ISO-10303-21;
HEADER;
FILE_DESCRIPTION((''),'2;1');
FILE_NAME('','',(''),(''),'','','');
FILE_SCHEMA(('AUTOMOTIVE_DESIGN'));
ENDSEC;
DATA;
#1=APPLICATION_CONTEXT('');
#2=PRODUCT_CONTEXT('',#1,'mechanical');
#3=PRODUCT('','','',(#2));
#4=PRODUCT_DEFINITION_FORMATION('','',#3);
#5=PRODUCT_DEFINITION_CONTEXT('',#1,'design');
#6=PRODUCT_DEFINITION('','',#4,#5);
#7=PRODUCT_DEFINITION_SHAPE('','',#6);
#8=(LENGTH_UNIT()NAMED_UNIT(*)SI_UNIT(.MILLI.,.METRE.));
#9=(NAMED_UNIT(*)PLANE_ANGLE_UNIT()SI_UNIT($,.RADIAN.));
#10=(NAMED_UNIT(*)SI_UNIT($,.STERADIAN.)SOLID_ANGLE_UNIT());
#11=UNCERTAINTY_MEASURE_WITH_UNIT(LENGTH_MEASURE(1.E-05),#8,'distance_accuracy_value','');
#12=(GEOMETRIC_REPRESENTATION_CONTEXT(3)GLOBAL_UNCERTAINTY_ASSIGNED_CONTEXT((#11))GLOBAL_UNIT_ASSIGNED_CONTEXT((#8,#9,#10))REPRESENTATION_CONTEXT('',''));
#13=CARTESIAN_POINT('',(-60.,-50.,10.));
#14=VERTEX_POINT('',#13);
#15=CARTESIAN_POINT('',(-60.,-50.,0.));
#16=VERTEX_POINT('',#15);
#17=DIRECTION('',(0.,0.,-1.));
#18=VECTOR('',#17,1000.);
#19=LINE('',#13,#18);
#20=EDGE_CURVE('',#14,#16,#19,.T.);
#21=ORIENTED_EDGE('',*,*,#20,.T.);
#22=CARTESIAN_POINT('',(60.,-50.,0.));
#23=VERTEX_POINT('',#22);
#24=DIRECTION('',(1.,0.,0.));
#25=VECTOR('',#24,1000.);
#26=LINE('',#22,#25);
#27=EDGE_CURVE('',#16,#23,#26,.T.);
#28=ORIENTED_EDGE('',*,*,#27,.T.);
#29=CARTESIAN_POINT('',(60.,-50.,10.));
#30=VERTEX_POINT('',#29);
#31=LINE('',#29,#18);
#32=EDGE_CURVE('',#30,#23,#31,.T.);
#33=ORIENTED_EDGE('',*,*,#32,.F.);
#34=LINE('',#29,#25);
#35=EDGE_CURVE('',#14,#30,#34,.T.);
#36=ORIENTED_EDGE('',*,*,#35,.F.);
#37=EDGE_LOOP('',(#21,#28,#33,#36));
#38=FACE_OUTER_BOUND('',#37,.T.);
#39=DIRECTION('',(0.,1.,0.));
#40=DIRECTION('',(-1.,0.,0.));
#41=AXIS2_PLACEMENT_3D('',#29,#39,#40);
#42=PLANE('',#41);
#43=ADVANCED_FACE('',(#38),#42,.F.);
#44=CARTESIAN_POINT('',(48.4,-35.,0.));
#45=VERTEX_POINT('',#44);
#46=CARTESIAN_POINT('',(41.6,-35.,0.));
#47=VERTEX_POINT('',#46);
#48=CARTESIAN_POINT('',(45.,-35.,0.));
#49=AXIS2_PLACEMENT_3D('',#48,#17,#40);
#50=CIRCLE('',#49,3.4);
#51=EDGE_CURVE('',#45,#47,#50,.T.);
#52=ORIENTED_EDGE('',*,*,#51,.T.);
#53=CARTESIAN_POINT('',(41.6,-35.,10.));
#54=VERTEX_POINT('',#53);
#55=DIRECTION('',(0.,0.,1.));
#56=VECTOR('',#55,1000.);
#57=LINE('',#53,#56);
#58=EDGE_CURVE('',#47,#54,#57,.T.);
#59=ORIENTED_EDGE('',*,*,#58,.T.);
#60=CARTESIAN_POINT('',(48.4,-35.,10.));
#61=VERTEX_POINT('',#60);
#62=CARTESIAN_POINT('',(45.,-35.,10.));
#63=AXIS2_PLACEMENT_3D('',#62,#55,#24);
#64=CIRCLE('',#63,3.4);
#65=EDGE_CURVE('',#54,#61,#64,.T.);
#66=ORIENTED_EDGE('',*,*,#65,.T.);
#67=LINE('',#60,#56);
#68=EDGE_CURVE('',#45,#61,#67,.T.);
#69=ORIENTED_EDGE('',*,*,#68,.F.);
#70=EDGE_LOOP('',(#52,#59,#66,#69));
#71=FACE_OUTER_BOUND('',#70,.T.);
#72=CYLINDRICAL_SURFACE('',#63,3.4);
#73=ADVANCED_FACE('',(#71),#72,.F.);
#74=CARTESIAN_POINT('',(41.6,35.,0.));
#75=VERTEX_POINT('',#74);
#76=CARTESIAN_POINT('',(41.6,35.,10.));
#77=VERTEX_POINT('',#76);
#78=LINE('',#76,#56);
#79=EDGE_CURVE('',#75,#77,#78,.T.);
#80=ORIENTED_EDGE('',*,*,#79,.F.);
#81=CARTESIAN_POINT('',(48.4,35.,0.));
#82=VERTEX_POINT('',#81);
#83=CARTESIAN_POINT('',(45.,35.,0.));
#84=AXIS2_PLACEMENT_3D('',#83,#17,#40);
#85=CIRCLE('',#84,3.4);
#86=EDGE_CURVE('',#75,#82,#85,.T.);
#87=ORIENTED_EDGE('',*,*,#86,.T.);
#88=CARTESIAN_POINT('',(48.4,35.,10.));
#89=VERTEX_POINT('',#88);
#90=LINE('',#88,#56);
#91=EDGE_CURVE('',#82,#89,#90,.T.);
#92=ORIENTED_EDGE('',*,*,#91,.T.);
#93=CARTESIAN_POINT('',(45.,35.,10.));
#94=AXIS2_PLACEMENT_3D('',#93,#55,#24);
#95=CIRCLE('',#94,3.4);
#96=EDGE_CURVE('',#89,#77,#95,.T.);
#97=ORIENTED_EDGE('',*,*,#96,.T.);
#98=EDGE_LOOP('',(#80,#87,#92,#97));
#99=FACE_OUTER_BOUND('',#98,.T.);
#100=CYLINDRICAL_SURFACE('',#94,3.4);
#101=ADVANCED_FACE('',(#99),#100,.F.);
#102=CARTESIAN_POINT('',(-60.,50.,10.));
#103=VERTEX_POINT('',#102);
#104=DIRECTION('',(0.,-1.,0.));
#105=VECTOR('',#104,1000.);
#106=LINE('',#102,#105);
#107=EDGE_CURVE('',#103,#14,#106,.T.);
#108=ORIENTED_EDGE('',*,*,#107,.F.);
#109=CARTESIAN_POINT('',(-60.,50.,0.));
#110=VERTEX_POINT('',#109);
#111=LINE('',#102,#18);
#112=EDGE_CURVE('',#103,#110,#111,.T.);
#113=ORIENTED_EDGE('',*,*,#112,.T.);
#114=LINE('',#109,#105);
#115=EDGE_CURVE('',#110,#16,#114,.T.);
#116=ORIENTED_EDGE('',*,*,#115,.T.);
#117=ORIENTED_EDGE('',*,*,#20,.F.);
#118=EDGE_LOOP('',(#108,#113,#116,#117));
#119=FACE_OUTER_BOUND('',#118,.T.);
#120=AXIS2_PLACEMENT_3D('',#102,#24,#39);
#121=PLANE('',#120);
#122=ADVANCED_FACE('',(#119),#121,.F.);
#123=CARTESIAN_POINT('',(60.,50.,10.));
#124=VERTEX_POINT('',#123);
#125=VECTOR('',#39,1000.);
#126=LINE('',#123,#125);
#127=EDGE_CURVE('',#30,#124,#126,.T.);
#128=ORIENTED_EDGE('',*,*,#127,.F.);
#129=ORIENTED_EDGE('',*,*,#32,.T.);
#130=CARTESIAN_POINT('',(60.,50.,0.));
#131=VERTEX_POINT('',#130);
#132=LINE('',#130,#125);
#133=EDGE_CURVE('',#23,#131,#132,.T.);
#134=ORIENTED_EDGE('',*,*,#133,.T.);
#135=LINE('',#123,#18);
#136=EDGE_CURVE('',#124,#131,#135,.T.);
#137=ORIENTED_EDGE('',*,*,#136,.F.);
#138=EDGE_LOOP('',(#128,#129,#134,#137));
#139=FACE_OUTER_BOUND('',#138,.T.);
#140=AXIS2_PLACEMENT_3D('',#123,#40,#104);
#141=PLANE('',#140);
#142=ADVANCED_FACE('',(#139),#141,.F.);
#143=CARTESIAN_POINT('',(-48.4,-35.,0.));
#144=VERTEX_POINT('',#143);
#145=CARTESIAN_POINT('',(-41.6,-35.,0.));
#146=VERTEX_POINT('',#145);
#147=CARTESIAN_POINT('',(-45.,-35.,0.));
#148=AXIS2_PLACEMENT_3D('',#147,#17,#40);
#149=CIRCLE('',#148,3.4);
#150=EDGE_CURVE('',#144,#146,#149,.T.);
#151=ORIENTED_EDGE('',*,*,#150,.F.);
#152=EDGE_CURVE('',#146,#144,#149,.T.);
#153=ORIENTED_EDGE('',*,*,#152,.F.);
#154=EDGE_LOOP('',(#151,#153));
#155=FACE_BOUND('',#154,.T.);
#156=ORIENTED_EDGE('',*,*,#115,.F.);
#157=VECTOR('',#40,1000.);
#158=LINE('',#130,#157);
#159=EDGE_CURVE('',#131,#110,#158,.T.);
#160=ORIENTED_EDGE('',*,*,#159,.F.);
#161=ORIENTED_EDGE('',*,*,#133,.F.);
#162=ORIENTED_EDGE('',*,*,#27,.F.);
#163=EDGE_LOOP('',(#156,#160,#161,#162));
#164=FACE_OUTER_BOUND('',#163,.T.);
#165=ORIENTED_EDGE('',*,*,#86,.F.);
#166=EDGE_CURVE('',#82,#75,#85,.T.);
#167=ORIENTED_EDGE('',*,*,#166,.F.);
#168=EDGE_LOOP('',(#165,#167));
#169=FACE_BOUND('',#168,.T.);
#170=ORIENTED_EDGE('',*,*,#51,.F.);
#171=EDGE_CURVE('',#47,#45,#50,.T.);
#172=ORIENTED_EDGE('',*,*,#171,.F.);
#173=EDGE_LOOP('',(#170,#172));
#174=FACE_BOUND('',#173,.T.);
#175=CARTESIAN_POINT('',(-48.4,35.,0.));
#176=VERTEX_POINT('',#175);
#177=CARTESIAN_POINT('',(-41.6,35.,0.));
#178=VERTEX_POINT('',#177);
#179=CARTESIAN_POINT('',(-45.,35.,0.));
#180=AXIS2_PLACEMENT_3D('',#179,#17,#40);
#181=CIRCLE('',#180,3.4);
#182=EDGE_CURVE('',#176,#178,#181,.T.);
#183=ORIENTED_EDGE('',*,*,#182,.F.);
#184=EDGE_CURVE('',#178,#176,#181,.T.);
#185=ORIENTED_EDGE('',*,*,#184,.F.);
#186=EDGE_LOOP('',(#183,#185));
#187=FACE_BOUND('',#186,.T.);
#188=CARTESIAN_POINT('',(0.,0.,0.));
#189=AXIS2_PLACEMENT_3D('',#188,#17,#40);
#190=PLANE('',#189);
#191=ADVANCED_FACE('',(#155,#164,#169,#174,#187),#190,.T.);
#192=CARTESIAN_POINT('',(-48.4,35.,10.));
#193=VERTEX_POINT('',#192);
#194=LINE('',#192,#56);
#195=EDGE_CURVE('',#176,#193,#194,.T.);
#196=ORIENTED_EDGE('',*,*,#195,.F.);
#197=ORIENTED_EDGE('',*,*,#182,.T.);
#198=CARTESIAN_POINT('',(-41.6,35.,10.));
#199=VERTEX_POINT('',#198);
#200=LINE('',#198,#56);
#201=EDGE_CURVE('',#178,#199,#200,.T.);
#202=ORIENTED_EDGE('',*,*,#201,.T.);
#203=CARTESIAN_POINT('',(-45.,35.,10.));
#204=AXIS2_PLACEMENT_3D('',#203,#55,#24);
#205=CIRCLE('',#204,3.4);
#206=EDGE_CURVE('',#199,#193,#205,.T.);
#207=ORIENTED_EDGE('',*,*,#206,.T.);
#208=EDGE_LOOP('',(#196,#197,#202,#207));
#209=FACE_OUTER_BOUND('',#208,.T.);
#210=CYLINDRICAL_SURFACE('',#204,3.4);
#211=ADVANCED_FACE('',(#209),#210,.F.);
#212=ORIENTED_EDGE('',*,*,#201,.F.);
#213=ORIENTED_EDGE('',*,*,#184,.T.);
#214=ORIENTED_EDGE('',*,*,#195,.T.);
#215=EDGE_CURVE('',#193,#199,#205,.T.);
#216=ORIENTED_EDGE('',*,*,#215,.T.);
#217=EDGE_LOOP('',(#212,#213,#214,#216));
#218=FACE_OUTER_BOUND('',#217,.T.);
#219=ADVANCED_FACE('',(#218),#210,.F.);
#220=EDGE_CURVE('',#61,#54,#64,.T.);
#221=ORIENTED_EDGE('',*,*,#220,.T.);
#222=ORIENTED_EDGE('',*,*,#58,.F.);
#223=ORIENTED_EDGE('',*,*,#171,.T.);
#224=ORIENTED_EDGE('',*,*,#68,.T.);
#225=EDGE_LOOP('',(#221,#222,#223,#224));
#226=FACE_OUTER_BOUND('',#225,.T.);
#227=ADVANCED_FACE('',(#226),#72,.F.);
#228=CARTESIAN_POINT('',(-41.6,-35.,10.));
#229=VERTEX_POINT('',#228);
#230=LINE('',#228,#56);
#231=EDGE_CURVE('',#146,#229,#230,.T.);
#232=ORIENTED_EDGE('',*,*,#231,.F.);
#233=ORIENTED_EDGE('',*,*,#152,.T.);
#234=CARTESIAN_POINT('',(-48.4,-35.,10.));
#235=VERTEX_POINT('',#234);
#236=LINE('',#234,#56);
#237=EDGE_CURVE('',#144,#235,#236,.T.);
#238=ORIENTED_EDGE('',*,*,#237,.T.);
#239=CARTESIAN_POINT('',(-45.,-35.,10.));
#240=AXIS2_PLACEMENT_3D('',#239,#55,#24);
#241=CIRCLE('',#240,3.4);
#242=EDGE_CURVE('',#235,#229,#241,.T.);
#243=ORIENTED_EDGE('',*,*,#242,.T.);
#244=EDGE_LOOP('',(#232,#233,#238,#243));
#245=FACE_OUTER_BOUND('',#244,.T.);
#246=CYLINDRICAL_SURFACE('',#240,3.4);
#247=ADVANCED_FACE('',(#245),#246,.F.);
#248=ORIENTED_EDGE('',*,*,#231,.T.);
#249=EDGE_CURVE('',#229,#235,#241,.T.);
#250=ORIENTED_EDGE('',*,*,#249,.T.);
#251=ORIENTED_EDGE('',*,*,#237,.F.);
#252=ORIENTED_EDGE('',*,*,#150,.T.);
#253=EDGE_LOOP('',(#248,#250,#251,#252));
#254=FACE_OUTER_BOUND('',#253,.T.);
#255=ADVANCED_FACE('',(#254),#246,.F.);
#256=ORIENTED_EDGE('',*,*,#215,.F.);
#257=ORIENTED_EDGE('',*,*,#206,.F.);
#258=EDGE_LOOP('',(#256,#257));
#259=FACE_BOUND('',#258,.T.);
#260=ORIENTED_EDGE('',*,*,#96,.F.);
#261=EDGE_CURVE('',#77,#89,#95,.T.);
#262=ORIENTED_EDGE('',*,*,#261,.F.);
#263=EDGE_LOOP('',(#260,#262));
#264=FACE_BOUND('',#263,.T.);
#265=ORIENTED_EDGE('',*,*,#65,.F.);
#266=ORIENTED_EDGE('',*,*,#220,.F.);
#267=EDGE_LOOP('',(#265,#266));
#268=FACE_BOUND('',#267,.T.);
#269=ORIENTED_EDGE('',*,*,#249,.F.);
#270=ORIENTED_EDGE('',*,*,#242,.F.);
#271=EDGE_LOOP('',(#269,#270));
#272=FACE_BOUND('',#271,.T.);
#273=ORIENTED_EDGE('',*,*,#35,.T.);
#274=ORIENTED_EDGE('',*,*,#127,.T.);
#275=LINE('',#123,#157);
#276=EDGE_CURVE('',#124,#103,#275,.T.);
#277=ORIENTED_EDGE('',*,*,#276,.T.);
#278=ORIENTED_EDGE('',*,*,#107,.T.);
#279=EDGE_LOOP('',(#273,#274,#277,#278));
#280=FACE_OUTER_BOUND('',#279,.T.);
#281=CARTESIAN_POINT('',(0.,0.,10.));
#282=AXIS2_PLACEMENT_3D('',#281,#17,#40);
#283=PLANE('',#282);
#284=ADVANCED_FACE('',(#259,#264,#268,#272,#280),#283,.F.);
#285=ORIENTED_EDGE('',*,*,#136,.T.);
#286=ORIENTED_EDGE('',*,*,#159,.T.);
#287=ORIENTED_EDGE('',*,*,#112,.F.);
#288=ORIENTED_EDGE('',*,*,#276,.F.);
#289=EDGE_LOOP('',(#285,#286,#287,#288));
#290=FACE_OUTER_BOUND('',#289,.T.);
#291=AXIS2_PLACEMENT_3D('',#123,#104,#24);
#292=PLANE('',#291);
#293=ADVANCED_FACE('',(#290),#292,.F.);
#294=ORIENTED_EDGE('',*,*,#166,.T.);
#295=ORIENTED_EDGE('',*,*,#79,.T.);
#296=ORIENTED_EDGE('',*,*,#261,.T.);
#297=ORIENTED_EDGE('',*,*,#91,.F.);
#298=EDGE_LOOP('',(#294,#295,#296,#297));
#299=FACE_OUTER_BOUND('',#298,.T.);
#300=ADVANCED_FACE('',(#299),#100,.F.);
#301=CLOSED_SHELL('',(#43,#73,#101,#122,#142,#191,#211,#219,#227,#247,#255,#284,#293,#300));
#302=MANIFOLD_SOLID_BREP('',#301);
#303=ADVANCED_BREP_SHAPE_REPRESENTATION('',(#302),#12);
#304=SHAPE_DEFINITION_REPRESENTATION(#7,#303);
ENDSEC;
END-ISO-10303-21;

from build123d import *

# Parameters (mm, degrees)
SKETCH1_W             = 120
SKETCH1_H             = 100
BOSS_EXTRUDE1_DEPTH   = 10
M8_TAPPED_HOLE1_D     = 6.8
M8_TAPPED_HOLE1_DEPTH = 19.75
M8_TAPPED_HOLE1_TIP   = 2.042926105


with BuildPart() as part:
    # Sketch1 → Boss-Extrude1 (new body)
    with BuildSketch(Plane.XY):
        Rectangle(SKETCH1_W, SKETCH1_H)
    extrude(amount=BOSS_EXTRUDE1_DEPTH)

    # M8 Tapped Hole1
    with Locations(Plane.XY.offset(10)):
        with Locations((45, -35), (-45, -35), (-45, 35), (45, 35)):
            Hole(M8_TAPPED_HOLE1_D / 2, depth=M8_TAPPED_HOLE1_DEPTH)
            with Locations((0, 0, -(M8_TAPPED_HOLE1_DEPTH + M8_TAPPED_HOLE1_TIP / 2))):  # 118° drill point
                Cone(0, M8_TAPPED_HOLE1_D / 2, M8_TAPPED_HOLE1_TIP, mode=Mode.SUBTRACT)


solid = part.part
